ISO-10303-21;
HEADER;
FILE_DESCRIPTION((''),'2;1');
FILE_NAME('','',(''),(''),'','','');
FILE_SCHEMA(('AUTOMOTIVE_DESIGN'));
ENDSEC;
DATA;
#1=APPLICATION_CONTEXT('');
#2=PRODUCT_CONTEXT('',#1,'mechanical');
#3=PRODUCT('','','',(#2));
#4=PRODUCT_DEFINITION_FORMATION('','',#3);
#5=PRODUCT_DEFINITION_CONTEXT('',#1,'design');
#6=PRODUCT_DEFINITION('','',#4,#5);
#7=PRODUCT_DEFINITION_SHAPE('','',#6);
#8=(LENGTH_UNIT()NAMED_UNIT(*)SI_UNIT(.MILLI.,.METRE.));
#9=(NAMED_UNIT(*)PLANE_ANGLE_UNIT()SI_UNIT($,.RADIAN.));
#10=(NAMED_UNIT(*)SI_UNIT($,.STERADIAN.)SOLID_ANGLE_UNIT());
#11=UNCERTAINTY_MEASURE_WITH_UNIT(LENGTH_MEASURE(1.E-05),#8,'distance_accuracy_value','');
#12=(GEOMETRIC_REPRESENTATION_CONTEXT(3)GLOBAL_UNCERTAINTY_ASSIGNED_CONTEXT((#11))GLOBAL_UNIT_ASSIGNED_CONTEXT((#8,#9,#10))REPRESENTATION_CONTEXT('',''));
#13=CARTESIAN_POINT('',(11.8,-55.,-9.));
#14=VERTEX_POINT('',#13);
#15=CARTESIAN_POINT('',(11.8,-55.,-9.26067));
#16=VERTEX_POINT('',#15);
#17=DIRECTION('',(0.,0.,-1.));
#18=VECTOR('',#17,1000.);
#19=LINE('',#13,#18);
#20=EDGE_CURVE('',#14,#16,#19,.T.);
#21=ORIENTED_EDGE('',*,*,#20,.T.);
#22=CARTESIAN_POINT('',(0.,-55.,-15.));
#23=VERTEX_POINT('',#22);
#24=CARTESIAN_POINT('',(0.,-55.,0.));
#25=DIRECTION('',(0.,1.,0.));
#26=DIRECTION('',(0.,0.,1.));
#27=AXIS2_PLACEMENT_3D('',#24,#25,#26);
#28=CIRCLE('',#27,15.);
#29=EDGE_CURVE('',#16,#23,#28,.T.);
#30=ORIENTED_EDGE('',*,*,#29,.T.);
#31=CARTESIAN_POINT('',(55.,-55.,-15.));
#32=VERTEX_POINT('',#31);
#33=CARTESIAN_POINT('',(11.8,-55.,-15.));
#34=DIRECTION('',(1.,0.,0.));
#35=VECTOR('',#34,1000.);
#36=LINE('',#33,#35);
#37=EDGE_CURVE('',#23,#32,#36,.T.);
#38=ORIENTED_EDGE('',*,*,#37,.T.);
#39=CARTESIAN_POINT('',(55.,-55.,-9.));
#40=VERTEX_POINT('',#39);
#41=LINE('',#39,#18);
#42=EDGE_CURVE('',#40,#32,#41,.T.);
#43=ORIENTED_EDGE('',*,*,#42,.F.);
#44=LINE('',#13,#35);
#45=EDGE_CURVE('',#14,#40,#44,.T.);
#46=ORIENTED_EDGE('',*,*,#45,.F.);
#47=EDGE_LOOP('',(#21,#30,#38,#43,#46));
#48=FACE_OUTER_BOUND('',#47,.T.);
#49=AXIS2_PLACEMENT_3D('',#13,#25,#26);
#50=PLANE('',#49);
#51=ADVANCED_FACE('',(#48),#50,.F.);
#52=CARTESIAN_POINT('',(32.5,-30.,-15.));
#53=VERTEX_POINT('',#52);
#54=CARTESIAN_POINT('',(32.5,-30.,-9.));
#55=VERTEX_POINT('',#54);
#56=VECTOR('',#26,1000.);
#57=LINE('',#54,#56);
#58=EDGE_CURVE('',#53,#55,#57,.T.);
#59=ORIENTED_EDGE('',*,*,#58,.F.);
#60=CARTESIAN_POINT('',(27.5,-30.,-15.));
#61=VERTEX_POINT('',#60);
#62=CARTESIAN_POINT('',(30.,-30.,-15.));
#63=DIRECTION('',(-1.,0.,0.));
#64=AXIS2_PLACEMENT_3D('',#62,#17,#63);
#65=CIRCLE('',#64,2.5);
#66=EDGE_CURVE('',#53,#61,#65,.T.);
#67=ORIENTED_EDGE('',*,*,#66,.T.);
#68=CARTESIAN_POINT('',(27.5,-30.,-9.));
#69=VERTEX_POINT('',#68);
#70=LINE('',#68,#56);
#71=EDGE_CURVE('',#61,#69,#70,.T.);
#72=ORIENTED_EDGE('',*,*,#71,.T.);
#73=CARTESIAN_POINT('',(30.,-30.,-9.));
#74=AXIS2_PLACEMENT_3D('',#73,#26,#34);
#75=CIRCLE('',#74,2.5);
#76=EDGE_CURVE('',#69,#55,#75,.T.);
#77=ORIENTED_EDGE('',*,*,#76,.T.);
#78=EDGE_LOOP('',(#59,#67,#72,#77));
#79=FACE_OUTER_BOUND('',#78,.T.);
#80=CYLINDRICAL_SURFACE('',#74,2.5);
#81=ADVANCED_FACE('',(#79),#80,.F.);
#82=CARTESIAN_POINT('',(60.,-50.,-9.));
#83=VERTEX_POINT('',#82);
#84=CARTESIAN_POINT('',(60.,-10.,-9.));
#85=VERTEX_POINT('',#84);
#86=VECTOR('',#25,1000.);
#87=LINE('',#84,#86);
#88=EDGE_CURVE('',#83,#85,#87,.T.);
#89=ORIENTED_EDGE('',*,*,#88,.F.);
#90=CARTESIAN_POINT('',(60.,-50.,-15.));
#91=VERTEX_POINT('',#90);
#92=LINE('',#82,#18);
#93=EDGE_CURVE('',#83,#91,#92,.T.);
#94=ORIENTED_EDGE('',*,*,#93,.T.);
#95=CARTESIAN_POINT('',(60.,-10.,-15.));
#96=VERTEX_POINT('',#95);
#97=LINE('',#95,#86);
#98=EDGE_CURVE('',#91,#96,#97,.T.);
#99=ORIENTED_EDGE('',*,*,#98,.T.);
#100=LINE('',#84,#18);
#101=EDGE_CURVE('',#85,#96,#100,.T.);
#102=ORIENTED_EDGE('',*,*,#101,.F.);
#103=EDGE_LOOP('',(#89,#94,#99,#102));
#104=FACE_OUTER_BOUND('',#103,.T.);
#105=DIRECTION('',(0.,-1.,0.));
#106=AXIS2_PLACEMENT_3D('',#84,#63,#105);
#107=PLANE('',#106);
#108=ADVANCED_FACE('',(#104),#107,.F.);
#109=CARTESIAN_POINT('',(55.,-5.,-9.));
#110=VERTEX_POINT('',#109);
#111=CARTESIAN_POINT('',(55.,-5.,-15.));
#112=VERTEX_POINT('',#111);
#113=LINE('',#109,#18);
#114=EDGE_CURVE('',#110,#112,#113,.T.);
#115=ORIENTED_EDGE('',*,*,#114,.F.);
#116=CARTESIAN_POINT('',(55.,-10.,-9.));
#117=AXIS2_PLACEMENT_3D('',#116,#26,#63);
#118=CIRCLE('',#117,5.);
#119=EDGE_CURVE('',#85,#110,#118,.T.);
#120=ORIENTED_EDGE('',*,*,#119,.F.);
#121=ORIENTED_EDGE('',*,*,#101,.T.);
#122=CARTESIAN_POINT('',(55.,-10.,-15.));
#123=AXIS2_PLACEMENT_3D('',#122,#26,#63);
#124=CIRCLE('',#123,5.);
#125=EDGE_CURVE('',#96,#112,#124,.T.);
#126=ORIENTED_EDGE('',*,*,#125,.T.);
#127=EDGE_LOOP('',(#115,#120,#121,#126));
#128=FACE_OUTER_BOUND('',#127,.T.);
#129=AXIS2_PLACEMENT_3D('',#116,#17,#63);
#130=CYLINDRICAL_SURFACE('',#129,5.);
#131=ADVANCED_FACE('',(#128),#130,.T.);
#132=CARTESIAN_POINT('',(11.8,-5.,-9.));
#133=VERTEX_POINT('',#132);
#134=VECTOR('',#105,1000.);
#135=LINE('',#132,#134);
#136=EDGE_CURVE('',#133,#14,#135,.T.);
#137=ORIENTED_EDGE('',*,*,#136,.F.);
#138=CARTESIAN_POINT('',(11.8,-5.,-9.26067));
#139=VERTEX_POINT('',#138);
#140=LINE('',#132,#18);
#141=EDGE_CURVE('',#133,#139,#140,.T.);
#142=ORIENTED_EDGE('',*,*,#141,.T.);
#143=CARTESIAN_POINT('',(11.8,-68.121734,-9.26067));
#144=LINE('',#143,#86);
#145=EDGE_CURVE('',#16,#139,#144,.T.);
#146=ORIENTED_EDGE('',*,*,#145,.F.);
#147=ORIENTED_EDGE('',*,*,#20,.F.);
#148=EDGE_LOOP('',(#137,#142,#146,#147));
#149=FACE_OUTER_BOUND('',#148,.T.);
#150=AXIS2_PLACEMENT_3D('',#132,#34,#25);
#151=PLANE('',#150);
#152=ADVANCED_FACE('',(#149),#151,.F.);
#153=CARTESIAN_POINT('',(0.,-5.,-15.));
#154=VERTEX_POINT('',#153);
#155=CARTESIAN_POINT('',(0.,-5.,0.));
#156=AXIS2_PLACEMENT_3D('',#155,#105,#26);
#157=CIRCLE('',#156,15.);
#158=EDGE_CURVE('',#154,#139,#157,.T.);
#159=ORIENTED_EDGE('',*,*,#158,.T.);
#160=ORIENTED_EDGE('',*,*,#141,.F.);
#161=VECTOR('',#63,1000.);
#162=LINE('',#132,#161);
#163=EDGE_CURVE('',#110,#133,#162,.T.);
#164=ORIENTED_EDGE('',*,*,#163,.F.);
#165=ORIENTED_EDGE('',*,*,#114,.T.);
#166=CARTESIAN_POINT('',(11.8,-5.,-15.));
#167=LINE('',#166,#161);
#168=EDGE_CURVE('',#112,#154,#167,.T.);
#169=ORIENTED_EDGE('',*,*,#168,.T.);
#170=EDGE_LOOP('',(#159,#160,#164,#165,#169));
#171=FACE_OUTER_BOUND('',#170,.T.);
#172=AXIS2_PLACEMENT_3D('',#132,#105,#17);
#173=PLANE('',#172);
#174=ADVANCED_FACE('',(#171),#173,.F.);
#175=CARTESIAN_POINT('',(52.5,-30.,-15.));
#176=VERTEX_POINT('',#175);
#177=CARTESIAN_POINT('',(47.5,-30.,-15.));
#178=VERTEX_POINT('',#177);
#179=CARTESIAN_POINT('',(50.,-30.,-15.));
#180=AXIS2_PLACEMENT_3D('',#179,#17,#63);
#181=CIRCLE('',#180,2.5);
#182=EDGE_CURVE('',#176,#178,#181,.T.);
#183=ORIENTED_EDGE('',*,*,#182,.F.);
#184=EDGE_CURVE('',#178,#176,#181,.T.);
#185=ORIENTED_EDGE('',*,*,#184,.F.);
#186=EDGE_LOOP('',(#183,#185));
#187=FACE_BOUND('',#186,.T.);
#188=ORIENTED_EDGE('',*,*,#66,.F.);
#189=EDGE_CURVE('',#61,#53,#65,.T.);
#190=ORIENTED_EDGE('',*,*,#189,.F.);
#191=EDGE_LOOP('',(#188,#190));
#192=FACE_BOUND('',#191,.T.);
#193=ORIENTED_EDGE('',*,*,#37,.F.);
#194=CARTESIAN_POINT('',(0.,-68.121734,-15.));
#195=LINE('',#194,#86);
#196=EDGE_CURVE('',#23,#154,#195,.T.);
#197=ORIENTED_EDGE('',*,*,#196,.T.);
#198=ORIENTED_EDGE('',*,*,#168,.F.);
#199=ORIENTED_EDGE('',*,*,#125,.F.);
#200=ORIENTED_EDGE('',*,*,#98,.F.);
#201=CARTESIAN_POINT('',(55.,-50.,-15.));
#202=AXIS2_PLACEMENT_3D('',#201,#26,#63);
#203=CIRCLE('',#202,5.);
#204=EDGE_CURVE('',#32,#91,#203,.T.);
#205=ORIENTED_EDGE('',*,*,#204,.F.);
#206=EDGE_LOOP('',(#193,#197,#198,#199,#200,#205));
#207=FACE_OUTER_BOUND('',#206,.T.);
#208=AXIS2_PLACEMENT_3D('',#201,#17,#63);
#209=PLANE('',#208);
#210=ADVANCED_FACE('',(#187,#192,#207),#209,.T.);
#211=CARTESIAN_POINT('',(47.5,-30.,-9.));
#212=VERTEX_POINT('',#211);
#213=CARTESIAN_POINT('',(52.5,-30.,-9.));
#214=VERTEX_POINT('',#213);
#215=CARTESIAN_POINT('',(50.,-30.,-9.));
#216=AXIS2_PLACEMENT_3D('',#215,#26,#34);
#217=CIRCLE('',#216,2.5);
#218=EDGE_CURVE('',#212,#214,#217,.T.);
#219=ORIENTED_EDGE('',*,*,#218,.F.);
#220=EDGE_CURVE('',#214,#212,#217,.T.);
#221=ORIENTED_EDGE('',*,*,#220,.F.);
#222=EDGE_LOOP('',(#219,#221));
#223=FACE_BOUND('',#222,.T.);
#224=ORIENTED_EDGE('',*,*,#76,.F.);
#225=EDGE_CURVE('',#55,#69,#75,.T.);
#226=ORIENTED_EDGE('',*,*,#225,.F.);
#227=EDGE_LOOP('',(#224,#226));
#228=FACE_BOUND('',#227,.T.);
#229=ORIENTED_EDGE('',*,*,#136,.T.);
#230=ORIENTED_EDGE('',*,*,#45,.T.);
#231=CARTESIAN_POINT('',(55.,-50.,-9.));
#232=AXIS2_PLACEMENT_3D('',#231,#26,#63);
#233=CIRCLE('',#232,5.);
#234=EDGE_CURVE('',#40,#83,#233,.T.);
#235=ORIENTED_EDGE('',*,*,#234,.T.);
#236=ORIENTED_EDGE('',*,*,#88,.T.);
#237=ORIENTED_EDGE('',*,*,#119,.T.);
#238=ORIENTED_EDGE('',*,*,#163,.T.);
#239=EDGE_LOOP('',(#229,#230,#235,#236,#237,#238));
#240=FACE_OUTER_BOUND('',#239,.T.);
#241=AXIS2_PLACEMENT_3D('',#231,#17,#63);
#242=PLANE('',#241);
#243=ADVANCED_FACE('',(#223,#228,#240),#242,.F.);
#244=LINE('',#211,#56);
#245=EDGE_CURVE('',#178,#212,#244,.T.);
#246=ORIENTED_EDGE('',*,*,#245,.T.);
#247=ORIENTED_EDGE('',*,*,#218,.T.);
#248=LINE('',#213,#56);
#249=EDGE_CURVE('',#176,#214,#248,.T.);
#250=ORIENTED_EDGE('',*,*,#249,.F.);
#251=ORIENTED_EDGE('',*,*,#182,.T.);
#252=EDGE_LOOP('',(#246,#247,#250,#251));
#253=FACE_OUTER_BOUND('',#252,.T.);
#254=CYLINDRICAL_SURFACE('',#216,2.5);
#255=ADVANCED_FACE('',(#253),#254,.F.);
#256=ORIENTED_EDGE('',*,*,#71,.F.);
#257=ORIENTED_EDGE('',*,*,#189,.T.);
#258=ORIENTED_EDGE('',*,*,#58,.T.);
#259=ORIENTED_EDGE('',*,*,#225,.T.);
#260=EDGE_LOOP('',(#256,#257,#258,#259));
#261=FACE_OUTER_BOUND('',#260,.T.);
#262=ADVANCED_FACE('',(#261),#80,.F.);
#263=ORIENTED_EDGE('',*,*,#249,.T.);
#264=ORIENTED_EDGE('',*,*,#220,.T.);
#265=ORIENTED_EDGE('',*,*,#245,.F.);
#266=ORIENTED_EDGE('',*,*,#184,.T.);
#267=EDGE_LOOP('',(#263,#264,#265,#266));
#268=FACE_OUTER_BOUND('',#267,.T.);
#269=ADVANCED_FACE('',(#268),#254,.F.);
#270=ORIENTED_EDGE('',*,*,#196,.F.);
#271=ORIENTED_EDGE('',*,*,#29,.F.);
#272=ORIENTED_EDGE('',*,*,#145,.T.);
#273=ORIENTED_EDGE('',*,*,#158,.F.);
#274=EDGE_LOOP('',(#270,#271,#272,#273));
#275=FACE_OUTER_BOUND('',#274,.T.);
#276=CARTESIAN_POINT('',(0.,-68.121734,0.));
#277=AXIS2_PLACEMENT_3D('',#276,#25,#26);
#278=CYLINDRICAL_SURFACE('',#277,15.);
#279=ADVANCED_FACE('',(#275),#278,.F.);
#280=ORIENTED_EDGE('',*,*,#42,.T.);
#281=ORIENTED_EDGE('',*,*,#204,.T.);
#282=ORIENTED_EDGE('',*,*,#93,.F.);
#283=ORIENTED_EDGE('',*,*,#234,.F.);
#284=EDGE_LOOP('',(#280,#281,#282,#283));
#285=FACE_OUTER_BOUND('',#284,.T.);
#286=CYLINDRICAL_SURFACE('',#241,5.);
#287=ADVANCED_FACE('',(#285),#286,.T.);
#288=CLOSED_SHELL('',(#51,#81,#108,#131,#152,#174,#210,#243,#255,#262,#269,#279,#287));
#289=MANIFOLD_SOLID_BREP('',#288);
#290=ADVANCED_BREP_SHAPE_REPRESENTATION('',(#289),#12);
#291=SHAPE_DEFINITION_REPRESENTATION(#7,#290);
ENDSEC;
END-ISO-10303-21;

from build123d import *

# Parameters (mm, degrees)
BOSS_EXTRUDE1_DEPTH   = 6
BOSS_EXTRUDE2_DEPTH   = 50
M6_TAPPED_HOLE1_D     = 5
M6_TAPPED_HOLE1_DEPTH = 15
M6_TAPPED_HOLE1_TIP   = 1.502151548


with BuildPart() as part:
    # Sketch1 → Boss-Extrude1 (new body)
    with BuildSketch(Plane.XY.offset(-15)):
        with BuildLine():
            Line((11.8, -5), (55, -5))
            ThreePointArc((55, -5), (58.535533906, -6.464466094), (60, -10))
            Line((60, -10), (60, -50))
            ThreePointArc((60, -50), (58.535533906, -53.535533906), (55, -55))
            Line((55, -55), (11.8, -55))
            Line((11.8, -55), (11.8, -5))
        make_face()
    extrude(amount=BOSS_EXTRUDE1_DEPTH)

    # Sketch2 → Boss-Extrude2 (add)
    with BuildSketch(Plane(origin=(0, -5, 0), x_dir=(1, 0, 0), z_dir=(0, 1, 0))):
        with BuildLine():
            Line((0, 15), (11.8, 15))
            Line((11.8, 15), (11.8, 9.260669522))
            ThreePointArc((11.8, 9.260669522), (6.560867213, 13.489070443), (0, 15))
        make_face()
    extrude(amount=-BOSS_EXTRUDE2_DEPTH)

    # M6 Tapped Hole1
    with Locations(Plane(origin=(50, -30, -9), x_dir=(1, 0, 0), z_dir=(0, 0, 1))):
        with Locations((0, 0), (-20, 0)):
            Hole(M6_TAPPED_HOLE1_D / 2, depth=M6_TAPPED_HOLE1_DEPTH)
            with Locations((0, 0, -(M6_TAPPED_HOLE1_DEPTH + M6_TAPPED_HOLE1_TIP / 2))):  # 118° drill point
                Cone(0, M6_TAPPED_HOLE1_D / 2, M6_TAPPED_HOLE1_TIP, mode=Mode.SUBTRACT)


solid = part.part
